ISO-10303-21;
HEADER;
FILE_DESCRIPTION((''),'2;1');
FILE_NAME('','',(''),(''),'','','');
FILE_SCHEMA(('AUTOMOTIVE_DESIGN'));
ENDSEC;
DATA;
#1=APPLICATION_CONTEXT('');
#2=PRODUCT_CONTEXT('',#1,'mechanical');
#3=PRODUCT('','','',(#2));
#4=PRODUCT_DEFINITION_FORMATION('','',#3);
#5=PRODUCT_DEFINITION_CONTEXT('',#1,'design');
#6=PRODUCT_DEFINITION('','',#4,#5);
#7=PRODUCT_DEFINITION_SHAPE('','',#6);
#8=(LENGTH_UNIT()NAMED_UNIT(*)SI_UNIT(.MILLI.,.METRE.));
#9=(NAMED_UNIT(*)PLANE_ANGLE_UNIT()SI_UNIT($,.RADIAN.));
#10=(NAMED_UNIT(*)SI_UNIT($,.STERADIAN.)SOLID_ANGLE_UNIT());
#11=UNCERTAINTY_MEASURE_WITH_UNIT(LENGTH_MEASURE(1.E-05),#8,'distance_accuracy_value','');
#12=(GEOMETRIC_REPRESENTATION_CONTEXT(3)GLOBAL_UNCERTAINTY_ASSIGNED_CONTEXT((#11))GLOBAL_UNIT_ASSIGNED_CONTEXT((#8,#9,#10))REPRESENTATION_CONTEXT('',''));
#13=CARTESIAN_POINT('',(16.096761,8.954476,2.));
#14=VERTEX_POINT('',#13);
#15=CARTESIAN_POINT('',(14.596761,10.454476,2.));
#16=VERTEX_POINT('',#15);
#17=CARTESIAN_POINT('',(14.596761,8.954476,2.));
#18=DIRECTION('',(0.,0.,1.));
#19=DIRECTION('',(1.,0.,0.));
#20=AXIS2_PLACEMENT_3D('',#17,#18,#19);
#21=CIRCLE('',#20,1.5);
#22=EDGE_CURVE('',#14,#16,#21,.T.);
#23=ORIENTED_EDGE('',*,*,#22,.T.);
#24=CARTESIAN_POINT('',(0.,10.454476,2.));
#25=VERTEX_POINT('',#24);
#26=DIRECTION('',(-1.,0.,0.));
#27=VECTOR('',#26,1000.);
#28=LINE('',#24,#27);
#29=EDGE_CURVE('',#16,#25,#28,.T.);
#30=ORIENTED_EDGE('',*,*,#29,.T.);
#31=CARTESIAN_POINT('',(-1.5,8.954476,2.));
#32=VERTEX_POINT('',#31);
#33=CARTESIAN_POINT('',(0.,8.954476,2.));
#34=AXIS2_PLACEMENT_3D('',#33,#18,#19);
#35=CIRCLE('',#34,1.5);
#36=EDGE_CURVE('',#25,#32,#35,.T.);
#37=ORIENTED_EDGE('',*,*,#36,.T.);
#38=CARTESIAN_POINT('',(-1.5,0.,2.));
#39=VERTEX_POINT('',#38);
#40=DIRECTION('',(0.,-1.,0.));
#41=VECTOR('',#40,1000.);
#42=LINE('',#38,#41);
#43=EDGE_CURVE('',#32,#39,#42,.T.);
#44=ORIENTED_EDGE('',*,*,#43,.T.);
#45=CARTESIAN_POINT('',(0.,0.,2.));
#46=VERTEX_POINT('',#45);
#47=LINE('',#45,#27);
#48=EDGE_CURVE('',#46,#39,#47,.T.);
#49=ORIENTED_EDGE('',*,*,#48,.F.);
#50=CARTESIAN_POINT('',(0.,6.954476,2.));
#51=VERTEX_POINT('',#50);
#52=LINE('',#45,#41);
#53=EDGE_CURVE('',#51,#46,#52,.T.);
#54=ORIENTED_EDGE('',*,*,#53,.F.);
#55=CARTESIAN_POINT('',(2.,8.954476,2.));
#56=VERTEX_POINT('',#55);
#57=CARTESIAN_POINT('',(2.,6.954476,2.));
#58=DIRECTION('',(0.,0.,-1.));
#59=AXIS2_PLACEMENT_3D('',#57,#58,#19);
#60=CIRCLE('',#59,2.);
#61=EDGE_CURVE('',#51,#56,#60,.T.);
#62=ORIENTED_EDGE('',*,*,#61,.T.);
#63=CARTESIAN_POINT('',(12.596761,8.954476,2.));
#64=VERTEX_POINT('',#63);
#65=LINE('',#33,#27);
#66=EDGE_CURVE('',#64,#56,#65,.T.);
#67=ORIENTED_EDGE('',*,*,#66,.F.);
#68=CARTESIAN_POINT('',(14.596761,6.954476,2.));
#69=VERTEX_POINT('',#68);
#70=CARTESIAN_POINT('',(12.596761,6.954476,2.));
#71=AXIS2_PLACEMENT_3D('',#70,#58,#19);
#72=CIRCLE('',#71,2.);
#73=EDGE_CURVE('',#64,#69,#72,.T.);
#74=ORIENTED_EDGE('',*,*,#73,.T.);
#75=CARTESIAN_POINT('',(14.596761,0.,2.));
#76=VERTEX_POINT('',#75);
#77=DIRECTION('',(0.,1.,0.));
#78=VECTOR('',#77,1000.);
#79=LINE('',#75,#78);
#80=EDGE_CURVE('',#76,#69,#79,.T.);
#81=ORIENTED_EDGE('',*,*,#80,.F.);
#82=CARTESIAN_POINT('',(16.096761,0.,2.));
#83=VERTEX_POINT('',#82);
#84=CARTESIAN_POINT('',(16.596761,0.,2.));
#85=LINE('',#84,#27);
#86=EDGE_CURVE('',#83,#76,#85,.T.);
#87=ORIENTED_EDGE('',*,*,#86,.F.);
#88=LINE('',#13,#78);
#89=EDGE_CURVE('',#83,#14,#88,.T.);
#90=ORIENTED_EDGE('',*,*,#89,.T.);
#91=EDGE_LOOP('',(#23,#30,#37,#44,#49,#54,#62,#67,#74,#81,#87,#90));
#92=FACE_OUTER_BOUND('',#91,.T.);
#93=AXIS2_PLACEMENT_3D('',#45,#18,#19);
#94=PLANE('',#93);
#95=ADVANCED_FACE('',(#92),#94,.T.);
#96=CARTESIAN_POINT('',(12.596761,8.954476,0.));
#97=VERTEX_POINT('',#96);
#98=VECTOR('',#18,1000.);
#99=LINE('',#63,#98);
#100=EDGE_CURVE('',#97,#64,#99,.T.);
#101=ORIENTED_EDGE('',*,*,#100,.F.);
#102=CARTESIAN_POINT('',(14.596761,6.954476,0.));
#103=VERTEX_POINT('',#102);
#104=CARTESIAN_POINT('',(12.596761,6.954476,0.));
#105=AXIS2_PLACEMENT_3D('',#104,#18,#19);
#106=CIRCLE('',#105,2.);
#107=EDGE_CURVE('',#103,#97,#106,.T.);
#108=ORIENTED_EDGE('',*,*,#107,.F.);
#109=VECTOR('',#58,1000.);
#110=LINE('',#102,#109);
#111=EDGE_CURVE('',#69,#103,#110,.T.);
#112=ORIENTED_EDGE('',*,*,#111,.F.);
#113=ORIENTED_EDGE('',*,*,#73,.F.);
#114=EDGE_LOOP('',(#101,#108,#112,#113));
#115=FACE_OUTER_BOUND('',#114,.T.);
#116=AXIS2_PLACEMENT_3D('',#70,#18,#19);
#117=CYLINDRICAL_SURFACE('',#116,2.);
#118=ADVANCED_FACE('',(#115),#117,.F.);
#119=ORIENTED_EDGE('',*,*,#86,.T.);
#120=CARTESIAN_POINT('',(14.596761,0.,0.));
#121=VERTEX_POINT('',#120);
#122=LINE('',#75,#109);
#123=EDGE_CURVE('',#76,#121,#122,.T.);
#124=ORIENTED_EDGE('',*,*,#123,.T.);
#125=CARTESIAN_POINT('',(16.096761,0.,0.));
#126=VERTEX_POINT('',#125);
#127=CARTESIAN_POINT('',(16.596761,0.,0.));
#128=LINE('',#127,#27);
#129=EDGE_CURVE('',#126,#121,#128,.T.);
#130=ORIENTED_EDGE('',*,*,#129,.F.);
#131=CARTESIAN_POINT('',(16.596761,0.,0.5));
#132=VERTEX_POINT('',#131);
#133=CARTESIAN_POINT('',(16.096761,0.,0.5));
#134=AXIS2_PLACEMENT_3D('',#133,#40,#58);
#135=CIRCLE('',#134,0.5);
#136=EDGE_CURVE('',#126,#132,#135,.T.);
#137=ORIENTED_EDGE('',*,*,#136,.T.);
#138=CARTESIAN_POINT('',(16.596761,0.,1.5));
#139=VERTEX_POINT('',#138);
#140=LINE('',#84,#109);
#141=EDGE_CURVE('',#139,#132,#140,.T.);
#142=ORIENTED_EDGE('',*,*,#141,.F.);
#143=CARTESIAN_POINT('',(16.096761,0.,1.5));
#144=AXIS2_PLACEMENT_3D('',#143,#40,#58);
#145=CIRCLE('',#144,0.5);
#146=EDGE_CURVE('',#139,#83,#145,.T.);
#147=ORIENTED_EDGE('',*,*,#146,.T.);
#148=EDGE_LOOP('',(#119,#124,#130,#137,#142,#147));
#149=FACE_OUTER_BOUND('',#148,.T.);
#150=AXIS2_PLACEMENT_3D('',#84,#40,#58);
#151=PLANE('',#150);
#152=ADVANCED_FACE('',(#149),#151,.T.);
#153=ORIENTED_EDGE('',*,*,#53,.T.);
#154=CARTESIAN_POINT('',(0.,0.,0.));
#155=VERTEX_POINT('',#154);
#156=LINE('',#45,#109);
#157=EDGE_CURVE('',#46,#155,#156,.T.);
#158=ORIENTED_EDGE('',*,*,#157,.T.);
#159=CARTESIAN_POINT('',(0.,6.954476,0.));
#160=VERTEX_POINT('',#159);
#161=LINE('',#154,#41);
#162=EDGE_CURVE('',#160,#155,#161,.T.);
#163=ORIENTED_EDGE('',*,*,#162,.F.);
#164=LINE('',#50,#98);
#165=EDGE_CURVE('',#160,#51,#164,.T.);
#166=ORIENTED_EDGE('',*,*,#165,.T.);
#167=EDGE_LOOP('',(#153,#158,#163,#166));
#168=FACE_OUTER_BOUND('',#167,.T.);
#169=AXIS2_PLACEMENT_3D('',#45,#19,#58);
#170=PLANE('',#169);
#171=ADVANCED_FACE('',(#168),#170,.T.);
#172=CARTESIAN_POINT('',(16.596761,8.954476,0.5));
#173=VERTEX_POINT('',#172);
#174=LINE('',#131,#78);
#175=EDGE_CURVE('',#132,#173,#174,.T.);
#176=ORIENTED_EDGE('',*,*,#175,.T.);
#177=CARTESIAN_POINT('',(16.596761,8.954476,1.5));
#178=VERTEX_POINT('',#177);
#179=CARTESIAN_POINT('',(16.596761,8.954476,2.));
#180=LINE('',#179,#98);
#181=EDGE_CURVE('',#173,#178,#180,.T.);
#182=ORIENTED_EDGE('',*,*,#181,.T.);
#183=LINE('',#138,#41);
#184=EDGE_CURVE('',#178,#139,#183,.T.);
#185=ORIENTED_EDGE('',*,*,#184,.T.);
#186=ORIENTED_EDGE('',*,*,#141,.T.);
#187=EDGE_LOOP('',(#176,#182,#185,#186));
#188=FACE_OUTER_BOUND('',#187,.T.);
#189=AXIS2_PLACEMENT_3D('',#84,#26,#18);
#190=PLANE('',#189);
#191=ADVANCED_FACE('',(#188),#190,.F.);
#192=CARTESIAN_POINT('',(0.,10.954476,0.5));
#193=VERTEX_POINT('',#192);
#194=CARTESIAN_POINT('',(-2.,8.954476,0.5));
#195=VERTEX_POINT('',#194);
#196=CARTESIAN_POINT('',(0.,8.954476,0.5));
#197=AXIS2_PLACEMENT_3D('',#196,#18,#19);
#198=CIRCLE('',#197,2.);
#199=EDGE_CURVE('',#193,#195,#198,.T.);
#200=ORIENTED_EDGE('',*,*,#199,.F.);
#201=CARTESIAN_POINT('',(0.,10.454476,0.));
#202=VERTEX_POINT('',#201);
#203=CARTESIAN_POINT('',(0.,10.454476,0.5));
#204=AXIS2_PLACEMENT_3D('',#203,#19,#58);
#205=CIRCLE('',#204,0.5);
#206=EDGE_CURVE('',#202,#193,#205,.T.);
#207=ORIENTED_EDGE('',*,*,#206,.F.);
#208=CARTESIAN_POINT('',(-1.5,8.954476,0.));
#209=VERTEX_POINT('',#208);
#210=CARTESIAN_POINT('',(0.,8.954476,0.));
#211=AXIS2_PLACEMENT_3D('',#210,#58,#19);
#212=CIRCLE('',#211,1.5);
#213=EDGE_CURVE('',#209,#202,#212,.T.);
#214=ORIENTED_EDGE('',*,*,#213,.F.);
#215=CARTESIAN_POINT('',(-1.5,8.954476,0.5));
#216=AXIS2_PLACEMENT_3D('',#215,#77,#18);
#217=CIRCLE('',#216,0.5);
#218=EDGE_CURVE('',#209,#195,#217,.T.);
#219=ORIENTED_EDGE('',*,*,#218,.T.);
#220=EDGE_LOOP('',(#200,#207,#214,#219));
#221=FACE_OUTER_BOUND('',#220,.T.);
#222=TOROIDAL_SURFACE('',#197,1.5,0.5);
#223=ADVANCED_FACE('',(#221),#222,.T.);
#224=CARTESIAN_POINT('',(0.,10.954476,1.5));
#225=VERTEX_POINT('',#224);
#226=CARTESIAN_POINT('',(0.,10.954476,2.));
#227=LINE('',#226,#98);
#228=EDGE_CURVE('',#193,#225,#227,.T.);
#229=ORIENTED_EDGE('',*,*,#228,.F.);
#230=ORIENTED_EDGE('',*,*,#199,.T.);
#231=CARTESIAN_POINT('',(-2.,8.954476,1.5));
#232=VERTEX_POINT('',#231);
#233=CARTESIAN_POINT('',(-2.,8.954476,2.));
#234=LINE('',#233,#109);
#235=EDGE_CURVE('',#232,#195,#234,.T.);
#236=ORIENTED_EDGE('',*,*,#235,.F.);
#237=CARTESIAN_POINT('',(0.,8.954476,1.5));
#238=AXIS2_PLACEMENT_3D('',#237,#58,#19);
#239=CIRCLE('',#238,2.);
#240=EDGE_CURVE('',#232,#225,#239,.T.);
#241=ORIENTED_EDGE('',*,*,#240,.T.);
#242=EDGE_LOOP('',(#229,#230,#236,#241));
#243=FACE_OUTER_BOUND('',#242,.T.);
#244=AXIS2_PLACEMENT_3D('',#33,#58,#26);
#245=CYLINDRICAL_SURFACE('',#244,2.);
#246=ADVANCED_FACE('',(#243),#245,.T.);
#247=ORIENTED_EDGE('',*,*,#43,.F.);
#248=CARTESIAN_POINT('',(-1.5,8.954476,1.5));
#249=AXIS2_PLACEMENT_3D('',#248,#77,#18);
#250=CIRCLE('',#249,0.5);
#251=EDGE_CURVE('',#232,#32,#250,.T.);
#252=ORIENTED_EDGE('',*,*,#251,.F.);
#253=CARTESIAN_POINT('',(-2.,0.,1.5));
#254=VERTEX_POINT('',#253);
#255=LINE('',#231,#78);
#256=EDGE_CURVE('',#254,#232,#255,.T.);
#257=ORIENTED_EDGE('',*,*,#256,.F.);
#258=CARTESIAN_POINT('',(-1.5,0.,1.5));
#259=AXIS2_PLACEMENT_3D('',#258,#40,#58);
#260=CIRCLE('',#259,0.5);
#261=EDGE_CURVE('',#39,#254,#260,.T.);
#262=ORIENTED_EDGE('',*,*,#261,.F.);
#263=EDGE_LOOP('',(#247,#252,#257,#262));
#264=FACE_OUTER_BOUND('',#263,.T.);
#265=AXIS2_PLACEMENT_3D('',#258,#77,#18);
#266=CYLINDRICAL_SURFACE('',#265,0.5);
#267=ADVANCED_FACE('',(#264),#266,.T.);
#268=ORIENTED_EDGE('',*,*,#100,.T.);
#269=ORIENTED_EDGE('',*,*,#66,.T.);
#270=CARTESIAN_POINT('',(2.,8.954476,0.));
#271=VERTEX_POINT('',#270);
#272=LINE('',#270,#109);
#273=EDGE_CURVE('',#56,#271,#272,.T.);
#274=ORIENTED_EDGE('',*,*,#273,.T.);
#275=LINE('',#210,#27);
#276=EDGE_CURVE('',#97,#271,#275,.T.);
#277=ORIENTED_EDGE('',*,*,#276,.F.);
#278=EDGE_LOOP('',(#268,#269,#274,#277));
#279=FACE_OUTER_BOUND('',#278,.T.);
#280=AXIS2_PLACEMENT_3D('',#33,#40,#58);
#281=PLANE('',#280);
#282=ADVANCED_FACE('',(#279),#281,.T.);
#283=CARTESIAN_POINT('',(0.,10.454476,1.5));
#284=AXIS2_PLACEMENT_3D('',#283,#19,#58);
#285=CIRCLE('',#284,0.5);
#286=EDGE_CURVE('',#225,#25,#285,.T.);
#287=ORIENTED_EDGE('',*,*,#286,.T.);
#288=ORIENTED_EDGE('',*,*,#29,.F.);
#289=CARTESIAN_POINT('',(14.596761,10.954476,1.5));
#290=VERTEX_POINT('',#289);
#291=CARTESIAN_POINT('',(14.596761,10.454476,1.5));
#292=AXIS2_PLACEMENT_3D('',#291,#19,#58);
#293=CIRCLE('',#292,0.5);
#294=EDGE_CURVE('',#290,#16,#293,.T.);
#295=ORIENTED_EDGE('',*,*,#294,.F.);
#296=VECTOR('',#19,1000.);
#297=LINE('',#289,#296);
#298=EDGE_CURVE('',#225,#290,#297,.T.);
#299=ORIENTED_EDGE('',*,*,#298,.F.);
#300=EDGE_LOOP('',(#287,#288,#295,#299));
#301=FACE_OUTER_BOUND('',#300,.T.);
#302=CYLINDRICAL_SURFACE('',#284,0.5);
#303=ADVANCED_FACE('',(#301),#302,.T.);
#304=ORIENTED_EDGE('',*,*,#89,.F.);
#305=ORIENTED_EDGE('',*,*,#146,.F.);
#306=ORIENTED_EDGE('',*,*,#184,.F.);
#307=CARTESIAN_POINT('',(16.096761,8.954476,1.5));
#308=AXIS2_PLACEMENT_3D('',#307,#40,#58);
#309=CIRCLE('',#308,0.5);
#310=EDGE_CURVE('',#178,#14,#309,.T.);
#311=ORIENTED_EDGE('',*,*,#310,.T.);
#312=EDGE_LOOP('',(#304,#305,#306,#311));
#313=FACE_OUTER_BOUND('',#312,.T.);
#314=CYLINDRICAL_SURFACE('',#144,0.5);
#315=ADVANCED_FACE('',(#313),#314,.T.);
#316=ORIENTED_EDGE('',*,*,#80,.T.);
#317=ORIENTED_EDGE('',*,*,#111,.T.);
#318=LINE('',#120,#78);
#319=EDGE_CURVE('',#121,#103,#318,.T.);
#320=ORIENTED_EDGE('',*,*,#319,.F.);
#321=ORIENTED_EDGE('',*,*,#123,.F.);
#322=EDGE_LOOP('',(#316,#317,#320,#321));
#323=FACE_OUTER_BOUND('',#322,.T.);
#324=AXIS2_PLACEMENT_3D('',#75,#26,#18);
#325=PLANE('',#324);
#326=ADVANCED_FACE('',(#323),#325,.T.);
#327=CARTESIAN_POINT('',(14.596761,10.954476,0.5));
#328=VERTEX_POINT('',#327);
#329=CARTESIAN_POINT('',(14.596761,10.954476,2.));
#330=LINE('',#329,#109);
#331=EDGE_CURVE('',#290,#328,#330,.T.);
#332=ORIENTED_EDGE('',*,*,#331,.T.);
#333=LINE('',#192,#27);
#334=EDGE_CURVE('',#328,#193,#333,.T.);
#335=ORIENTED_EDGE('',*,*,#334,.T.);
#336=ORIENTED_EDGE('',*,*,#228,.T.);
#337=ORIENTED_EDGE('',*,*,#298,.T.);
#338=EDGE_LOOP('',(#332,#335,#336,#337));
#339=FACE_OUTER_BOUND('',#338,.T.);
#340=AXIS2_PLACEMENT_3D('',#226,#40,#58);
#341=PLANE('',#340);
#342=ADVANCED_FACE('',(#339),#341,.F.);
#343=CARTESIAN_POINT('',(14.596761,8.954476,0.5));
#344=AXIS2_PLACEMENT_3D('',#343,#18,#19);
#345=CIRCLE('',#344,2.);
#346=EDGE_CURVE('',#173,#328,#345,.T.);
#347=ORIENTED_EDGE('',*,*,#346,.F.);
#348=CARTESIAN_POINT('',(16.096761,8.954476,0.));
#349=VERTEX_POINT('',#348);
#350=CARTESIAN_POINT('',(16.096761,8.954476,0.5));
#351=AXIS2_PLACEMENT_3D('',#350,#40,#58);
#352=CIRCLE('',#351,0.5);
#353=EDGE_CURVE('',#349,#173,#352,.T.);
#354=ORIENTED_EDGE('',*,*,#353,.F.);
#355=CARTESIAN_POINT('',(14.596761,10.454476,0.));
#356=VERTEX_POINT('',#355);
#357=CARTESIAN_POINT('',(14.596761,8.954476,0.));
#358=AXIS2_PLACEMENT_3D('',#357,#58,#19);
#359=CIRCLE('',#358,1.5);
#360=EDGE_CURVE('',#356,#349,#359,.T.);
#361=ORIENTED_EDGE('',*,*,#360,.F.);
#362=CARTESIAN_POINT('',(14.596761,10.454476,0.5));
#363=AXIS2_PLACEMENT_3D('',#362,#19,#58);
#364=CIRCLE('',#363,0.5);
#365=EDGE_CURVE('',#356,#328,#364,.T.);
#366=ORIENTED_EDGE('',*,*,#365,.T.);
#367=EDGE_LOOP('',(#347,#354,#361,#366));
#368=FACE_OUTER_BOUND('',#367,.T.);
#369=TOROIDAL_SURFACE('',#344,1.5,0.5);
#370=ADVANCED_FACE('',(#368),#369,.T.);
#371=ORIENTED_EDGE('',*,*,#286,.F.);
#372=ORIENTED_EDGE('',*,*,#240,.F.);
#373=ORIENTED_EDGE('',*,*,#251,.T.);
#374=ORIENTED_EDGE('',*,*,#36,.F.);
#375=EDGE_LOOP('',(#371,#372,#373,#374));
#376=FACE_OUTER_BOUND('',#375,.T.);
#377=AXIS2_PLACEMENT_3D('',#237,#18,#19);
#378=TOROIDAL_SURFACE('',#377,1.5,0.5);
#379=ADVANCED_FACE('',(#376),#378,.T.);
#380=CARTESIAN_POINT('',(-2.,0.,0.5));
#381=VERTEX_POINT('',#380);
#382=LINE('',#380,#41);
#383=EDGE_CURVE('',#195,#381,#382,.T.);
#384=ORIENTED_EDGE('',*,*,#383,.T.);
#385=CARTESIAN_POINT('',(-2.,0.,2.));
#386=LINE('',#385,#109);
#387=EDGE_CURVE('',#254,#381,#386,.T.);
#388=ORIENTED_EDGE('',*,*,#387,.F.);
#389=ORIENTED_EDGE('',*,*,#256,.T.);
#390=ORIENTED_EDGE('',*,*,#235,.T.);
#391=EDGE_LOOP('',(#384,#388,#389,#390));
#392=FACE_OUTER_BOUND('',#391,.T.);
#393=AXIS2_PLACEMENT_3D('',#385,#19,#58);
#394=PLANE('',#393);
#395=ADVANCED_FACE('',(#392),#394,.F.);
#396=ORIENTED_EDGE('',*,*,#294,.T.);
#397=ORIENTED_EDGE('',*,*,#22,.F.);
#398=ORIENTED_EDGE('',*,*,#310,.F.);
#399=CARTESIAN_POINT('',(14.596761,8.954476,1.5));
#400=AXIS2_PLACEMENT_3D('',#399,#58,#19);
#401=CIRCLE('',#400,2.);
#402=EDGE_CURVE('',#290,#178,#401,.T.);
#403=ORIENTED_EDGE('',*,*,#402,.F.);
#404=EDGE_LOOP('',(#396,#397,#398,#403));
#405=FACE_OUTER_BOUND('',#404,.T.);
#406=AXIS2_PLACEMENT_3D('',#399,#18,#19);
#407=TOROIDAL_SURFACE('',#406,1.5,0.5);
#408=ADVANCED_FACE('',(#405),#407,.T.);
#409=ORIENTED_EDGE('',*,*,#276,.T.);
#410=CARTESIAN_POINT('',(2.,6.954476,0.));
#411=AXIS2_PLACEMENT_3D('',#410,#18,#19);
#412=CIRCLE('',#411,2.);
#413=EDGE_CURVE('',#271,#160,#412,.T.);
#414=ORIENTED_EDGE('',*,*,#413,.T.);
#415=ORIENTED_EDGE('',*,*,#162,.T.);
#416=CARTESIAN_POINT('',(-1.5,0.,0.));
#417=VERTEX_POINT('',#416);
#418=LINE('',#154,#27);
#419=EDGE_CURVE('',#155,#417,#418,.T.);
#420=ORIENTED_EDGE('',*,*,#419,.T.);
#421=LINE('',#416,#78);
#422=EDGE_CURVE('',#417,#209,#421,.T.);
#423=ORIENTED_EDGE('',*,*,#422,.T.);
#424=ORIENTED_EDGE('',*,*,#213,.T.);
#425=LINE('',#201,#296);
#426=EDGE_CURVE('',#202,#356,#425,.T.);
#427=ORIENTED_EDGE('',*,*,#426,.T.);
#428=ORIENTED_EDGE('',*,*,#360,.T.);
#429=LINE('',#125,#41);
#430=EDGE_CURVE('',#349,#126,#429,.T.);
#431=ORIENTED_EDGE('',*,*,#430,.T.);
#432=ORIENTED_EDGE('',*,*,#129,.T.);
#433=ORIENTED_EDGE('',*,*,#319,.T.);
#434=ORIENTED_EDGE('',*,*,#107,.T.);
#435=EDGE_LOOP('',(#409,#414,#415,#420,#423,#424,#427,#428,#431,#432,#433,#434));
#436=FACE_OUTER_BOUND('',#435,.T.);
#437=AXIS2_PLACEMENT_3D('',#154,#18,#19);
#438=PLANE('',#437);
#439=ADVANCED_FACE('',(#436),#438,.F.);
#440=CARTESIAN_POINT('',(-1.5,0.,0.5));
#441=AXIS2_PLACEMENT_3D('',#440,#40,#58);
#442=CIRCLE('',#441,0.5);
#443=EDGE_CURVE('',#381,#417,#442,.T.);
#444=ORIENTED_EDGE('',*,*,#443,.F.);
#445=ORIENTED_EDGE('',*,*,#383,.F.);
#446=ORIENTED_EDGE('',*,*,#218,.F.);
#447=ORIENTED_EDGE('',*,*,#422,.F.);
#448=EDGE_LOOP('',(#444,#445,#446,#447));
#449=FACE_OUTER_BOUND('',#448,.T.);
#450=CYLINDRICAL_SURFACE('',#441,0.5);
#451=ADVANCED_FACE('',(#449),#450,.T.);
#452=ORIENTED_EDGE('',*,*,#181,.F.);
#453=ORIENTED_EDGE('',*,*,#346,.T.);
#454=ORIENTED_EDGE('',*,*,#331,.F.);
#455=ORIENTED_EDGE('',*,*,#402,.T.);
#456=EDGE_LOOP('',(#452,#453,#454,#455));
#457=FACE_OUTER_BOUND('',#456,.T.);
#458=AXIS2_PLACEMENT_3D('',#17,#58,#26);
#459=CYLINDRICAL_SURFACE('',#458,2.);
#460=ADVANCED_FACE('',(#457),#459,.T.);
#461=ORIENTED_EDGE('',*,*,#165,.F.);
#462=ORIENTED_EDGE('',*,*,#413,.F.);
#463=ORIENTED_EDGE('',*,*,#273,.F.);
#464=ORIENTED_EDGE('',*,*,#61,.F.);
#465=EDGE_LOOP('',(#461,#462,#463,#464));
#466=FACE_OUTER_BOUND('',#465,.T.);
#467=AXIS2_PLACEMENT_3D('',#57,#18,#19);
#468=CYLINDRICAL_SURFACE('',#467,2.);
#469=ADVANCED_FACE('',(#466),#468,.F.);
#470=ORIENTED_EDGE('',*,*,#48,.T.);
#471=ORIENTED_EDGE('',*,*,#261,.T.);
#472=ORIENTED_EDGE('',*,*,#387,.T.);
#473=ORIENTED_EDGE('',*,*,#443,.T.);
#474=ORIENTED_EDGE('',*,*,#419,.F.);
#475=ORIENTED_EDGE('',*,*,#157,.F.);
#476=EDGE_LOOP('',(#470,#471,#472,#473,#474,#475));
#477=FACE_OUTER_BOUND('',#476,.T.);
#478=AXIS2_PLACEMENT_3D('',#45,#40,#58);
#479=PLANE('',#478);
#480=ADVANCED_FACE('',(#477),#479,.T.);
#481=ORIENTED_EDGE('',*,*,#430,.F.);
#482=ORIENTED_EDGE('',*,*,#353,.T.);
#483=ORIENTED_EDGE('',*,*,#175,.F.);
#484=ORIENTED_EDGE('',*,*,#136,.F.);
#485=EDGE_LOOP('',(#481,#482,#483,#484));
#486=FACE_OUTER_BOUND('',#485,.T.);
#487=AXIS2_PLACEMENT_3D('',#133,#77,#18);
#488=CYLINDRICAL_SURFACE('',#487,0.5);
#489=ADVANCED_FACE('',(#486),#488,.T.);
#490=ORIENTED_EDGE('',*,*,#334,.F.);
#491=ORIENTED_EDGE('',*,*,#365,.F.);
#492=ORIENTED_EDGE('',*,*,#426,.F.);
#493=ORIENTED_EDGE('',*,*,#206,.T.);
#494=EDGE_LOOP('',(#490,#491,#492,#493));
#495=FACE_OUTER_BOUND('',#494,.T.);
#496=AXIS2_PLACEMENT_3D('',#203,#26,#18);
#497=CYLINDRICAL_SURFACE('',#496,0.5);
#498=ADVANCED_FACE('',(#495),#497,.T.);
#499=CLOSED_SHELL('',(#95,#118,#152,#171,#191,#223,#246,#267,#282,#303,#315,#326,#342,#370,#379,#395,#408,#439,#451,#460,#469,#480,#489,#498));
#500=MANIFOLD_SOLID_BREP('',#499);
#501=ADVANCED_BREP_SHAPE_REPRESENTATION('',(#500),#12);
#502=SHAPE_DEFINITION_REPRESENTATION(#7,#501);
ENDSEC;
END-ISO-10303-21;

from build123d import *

# Parameters (mm, degrees)
EXTRUDE_THIN1_DEPTH = 2
FILLET1_R           = 2
FILLET2_R           = 0.5


with BuildPart() as part:
    # Sketch1 → Extrude-Thin1 (new body)
    with BuildSketch(Plane.XY):
        Polygon((0, 0), (0, 8.954475992), (14.596760519, 8.954475992), (14.596760519, 0), (16.596760519, 0), (16.596760519, 10.954475992), (-2, 10.954475992), (-2, 0), align=None)
    extrude(amount=EXTRUDE_THIN1_DEPTH)

    # Fillet1
    fillet1_edges = [part.edges().sort_by_distance(p)[0] for p in [
        (-2, 10.954475992, 1),
        (16.596760519, 10.954475992, 1),
        (14.596760519, 8.954475992, 1),
        (0, 8.954475992, 1),
    ]]
    fillet(fillet1_edges, radius=FILLET1_R)

    # Fillet2
    fillet2_edges = [part.edges().sort_by_distance(p)[0] for p in [
        (16.596760519, 4.477237996, 2),
        (7.29838026, 10.954475992, 0),
        (7.29838026, 10.954475992, 2),
        (-2, 4.477237996, 0),
        (-1.414213562, 10.368689555, 0),
        (16.010974082, 10.368689555, 0),
        (-2, 4.477237996, 2),
        (-1.414213562, 10.368689555, 2),
        (16.010974082, 10.368689555, 2),
        (16.596760519, 4.477237996, 0),
    ]]
    fillet(fillet2_edges, radius=FILLET2_R)


solid = part.part
